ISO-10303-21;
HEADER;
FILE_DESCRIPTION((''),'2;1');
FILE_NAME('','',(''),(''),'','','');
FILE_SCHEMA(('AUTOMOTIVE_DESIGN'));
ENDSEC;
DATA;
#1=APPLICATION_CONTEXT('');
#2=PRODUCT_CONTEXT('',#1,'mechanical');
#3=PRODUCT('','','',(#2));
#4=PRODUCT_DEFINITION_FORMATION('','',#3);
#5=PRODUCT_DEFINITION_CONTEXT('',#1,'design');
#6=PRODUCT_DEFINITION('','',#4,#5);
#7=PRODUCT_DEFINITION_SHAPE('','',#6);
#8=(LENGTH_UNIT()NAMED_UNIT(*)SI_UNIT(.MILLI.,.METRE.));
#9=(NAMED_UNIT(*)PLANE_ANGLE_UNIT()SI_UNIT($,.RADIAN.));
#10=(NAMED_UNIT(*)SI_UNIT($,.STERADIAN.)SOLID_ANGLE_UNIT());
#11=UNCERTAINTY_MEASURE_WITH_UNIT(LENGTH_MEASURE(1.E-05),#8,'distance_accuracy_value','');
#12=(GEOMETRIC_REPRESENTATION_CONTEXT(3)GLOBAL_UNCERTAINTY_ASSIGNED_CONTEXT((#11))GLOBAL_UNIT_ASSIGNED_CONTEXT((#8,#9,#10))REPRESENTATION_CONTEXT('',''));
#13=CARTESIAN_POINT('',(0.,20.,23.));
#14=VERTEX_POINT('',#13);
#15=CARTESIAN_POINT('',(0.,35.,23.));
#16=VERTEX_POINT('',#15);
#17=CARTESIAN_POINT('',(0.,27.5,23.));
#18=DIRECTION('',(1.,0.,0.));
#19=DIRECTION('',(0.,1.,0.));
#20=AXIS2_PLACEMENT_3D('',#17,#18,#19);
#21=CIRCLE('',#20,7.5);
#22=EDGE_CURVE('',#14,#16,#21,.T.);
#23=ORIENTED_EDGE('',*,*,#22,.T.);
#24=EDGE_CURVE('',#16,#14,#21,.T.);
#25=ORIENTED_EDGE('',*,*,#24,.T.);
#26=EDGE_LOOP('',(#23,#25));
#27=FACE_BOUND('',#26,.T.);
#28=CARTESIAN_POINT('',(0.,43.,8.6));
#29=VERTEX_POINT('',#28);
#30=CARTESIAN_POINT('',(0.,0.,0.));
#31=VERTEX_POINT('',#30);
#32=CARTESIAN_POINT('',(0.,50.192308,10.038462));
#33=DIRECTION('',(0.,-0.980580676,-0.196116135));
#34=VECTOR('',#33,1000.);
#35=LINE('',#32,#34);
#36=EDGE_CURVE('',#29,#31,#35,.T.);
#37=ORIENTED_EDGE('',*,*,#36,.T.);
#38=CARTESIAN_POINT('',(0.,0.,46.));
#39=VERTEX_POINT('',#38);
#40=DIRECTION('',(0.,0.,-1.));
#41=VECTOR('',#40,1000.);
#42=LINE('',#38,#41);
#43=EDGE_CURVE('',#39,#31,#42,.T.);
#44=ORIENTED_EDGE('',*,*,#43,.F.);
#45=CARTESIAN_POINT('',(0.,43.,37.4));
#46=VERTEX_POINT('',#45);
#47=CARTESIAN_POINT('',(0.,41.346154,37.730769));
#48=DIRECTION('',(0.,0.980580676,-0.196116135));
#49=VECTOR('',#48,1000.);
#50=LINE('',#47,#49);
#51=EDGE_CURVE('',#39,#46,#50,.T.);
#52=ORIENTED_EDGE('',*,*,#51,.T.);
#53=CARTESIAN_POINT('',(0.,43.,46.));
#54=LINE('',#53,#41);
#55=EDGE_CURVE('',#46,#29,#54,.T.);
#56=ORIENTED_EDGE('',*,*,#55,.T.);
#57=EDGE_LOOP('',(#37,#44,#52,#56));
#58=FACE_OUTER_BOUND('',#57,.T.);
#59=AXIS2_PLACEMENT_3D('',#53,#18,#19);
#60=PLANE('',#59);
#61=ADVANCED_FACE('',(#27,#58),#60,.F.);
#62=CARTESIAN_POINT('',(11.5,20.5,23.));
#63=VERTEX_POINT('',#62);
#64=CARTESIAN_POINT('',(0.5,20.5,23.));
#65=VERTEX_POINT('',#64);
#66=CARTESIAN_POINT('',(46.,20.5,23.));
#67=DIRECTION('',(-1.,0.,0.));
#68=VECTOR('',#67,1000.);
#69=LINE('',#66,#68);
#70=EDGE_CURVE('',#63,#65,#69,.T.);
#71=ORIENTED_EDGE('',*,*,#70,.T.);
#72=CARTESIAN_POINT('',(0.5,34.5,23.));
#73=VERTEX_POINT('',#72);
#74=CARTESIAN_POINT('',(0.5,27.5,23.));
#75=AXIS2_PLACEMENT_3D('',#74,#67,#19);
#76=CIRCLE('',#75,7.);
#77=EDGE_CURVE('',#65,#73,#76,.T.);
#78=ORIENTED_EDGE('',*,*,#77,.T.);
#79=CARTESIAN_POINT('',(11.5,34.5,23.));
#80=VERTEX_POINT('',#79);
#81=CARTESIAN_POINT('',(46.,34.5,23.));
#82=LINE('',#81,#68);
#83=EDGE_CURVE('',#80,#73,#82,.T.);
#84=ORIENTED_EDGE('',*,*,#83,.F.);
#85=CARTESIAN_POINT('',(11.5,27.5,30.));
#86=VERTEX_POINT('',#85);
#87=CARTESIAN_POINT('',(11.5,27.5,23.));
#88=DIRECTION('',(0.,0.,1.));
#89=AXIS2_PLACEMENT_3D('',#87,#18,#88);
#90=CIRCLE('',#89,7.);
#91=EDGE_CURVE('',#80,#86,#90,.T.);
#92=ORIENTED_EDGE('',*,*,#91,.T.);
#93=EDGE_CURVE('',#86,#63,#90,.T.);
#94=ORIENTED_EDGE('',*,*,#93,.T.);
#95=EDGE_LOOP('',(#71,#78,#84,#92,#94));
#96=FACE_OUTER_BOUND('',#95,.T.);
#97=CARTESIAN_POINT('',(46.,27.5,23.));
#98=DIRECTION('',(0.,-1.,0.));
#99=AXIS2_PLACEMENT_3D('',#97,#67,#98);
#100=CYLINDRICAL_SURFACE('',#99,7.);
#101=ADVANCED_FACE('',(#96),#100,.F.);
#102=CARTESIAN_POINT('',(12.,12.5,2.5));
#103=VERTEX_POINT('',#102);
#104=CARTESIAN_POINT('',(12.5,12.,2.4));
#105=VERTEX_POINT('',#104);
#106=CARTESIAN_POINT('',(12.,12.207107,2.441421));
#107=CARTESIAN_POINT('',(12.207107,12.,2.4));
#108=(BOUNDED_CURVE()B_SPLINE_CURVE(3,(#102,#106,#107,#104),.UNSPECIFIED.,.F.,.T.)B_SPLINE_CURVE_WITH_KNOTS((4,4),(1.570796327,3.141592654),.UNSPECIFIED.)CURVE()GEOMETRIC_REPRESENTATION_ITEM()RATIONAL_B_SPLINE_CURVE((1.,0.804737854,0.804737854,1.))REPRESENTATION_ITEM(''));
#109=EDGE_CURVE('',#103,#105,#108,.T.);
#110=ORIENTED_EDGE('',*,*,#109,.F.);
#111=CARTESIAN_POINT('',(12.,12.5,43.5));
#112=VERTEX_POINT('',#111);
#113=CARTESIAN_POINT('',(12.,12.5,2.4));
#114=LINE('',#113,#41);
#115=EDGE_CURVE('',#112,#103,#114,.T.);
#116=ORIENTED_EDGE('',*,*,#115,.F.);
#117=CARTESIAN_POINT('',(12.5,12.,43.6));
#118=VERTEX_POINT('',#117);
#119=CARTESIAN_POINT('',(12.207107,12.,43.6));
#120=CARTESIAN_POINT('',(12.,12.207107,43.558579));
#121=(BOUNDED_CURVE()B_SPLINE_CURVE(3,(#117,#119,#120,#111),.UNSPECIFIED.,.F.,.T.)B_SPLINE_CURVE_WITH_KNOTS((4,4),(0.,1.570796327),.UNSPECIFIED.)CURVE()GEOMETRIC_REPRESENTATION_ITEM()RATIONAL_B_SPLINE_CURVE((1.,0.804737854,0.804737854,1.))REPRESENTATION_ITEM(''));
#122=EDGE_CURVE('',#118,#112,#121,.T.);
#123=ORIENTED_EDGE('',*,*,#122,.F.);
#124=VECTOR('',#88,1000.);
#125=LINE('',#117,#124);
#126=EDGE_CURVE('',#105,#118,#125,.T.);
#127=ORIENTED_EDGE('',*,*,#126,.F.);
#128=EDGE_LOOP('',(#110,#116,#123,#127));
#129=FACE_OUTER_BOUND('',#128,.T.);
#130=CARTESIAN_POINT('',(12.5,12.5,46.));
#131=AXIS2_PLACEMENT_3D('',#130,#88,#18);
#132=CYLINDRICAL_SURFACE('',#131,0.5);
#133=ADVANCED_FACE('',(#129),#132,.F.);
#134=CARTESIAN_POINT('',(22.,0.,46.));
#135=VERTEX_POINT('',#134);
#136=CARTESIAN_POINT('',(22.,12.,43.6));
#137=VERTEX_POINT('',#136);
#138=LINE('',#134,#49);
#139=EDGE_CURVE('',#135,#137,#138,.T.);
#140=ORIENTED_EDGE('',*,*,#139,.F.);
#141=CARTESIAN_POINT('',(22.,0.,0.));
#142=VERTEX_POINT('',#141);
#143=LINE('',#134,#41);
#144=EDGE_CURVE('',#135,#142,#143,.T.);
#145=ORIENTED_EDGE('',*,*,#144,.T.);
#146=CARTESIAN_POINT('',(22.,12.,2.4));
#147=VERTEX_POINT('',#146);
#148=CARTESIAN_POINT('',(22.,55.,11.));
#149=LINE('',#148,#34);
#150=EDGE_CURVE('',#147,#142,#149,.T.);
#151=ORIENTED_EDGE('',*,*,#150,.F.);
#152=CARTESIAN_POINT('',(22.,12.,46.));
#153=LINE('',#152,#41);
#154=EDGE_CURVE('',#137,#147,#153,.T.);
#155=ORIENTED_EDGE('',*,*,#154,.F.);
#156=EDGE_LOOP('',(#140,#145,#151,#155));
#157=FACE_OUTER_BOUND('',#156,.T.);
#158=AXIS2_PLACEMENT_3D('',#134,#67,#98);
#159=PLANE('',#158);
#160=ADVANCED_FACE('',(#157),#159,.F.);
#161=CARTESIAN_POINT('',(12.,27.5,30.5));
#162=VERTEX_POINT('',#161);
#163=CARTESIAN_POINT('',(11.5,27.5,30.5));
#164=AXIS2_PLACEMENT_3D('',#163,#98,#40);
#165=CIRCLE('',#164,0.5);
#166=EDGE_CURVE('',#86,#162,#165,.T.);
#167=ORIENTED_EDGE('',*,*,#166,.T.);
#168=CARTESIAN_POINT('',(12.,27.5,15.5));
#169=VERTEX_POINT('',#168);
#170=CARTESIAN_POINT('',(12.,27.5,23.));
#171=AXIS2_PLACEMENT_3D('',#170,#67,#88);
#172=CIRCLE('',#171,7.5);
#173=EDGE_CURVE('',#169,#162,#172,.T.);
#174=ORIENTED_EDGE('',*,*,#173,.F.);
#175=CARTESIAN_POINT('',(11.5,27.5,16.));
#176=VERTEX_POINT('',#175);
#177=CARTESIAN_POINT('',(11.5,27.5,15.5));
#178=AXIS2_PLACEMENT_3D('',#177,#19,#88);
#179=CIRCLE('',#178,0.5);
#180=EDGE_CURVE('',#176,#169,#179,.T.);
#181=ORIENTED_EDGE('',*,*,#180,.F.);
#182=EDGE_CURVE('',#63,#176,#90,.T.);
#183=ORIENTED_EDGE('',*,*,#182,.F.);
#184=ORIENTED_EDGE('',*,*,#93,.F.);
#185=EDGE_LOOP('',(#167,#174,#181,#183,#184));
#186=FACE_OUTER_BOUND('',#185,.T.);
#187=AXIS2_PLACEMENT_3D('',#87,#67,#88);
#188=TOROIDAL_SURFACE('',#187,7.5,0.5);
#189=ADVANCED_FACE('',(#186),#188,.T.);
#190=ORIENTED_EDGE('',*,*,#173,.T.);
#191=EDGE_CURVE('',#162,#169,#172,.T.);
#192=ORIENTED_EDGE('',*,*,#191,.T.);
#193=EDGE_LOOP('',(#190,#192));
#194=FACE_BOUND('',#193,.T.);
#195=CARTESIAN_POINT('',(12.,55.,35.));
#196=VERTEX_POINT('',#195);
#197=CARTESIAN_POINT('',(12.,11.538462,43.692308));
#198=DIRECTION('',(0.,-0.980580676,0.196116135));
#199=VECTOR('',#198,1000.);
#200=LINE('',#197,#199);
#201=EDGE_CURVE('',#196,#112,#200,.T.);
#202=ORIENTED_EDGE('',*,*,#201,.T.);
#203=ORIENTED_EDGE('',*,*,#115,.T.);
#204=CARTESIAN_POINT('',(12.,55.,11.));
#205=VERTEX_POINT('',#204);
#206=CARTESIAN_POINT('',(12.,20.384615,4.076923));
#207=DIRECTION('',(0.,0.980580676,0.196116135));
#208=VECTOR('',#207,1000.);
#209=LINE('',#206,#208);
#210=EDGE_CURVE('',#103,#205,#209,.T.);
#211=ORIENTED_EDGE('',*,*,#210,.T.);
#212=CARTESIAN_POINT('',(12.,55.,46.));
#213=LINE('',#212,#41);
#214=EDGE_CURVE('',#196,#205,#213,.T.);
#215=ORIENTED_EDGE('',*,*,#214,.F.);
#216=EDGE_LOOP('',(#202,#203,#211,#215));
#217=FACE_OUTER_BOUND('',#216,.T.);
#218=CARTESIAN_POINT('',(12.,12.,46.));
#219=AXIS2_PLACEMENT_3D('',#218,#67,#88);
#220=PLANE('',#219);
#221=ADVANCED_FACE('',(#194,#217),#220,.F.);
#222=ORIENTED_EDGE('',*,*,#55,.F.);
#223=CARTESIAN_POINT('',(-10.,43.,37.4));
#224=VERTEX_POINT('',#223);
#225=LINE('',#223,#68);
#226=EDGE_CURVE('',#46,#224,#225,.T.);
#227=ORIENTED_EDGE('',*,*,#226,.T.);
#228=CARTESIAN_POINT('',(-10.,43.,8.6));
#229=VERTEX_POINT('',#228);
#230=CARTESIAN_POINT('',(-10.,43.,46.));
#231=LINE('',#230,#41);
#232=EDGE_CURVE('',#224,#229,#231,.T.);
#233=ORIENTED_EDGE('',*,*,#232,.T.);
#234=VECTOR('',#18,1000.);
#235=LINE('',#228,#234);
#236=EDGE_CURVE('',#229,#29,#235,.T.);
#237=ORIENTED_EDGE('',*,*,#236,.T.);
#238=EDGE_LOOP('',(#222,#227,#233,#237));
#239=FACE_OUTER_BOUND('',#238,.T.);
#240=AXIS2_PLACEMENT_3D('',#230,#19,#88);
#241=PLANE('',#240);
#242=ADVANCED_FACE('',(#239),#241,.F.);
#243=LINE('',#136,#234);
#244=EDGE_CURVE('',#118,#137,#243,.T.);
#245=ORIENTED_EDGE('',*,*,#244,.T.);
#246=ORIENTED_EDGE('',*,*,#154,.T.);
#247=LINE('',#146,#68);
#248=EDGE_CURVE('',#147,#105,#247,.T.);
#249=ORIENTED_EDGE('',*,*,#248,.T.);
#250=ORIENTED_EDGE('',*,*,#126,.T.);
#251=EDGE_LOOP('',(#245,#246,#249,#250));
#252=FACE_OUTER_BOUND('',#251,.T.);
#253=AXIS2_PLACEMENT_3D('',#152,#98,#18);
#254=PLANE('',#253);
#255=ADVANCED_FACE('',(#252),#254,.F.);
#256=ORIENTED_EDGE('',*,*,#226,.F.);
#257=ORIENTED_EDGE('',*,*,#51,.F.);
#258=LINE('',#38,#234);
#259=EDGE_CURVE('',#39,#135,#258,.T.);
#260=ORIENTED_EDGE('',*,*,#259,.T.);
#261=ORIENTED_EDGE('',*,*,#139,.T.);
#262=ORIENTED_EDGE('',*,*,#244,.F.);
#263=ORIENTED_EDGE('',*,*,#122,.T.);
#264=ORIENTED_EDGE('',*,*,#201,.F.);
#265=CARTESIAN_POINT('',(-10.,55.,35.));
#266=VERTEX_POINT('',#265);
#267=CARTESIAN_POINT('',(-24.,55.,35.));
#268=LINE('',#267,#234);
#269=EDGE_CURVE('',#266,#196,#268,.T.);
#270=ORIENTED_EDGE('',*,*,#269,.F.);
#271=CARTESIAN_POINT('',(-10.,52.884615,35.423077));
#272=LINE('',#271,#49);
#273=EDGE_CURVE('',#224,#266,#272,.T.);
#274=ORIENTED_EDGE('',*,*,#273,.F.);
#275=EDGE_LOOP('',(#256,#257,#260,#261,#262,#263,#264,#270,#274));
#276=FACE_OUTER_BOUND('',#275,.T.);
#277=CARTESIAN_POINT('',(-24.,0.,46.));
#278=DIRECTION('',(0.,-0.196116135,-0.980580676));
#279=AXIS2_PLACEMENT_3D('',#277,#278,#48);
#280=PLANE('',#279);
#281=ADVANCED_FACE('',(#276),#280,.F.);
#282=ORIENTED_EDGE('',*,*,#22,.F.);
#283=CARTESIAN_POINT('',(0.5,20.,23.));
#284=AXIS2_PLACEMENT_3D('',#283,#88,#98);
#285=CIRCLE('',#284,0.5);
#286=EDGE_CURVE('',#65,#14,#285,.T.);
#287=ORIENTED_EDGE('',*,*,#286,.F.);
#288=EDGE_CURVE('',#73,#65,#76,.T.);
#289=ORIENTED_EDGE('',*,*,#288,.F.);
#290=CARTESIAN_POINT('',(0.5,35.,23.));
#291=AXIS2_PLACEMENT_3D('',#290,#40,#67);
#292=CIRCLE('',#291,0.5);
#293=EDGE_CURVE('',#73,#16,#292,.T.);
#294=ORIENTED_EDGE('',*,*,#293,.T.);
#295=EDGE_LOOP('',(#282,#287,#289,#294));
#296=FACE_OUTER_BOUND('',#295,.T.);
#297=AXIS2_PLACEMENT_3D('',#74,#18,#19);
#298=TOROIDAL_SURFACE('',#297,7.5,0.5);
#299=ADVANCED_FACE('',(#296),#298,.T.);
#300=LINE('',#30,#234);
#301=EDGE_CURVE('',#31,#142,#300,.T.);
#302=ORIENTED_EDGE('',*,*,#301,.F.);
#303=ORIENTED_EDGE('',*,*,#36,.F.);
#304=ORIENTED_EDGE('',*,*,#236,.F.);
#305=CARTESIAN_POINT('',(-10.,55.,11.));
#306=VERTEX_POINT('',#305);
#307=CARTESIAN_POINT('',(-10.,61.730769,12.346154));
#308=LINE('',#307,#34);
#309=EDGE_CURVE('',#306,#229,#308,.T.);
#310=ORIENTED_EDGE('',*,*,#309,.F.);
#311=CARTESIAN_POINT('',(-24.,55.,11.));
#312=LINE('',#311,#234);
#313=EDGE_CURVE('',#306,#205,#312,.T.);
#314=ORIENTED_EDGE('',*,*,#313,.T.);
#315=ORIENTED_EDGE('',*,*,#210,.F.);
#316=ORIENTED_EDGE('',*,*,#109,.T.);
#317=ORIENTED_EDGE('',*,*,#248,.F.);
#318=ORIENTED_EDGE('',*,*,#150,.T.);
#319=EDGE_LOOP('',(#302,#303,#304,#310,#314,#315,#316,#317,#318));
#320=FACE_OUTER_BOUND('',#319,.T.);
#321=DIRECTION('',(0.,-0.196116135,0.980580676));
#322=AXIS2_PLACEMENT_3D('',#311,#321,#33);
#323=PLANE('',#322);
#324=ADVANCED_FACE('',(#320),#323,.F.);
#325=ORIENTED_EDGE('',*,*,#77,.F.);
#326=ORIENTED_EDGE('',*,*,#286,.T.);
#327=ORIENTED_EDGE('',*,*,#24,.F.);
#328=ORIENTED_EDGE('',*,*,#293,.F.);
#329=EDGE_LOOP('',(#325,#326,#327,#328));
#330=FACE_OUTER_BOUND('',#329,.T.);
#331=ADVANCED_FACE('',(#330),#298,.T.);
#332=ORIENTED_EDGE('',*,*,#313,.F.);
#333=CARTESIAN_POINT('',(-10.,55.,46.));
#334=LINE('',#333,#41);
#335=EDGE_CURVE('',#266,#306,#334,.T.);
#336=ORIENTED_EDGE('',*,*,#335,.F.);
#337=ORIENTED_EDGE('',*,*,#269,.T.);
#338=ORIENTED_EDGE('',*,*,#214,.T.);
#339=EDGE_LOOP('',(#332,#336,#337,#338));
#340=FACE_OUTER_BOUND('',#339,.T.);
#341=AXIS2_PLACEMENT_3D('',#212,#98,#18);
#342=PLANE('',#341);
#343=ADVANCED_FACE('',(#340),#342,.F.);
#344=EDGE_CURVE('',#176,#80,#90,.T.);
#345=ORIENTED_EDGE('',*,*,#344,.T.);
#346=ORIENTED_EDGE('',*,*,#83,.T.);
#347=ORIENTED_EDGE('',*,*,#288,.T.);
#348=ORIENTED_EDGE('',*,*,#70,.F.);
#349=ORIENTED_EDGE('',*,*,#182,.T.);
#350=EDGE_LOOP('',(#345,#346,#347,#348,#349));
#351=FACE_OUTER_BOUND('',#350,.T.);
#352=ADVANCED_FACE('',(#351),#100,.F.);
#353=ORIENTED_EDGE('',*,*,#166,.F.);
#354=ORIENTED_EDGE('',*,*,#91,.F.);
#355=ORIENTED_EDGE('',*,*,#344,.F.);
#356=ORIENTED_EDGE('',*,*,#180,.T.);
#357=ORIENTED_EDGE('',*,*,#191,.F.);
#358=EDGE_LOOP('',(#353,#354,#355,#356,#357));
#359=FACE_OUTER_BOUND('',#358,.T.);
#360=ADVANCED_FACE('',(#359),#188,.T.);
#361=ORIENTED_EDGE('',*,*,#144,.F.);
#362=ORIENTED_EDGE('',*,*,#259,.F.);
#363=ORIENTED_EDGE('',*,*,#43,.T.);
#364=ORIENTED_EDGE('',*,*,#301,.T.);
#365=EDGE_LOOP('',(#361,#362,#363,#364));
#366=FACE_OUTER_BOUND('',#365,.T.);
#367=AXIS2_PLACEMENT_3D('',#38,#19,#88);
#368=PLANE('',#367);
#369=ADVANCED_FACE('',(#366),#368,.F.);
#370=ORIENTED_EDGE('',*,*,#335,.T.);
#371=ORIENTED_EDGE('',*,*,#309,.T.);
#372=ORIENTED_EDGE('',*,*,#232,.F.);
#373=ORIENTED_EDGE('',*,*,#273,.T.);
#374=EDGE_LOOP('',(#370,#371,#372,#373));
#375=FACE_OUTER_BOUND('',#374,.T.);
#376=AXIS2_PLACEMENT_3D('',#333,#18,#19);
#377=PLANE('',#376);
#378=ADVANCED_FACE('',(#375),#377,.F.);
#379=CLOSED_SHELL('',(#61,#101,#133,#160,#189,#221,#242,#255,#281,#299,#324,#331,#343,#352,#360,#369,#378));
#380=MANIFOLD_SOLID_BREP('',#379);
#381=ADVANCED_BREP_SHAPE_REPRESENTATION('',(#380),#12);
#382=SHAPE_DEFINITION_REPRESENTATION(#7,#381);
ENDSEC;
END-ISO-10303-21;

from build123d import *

# Parameters (mm, degrees)
BRACKET_BODY_DEPTH        = 46
TAPERED_SIDE_CUT_DEPTH    = 46
BORE_SKETCH_R             = 7
THROUGH_BORE_14_DEPTH     = 46
BORE_EDGE_FILLET_R0_5_A_R = 0.5
BORE_EDGE_FILLET_R0_5_B_R = 0.5
STEP_EDGE_FILLET_R0_5_R   = 0.5


with BuildPart() as part:
    # Bracket Profile Sketch → Bracket Body (new body)
    with BuildSketch(Plane.XY):
        Polygon((0, 0), (22, 0), (22, 12), (12, 12), (12, 55), (-10, 55), (-10, 43), (0, 43), align=None)
    extrude(amount=BRACKET_BODY_DEPTH)

    # Taper Cut Sketch → Tapered Side Cut (cut)
    with BuildSketch(Plane(origin=(22, 0, 0), x_dir=(0, 0, -1), z_dir=(1, 0, 0))):
        Polygon((-46, 0), (-35, 55), (-46, 55), align=None)
        Polygon((0, 0), (0, 55), (-11, 55), align=None)
    extrude(amount=-TAPERED_SIDE_CUT_DEPTH, mode=Mode.SUBTRACT)

    # Bore Sketch → Through Bore Ø14 (cut)
    with BuildSketch(Plane.ZY):
        with Locations(Location((23, 27.5, 0), (0, 0, 270))):
            Circle(BORE_SKETCH_R)
    extrude(amount=-THROUGH_BORE_14_DEPTH, mode=Mode.SUBTRACT)

    # Bore Edge Fillet R0.5 A
    bore_edge_fillet_r0_5_a_edges = [part.edges().sort_by_distance(p)[0] for p in [
        (12, 34.5, 23),
    ]]
    fillet(bore_edge_fillet_r0_5_a_edges, radius=BORE_EDGE_FILLET_R0_5_A_R)

    # Bore Edge Fillet R0.5 B
    bore_edge_fillet_r0_5_b_edges = [part.edges().sort_by_distance(p)[0] for p in [
        (0, 34.5, 23),
    ]]
    fillet(bore_edge_fillet_r0_5_b_edges, radius=BORE_EDGE_FILLET_R0_5_B_R)

    # Step Edge Fillet R0.5
    step_edge_fillet_r0_5_edges = [part.edges().sort_by_distance(p)[0] for p in [
        (12, 12, 23),
    ]]
    fillet(step_edge_fillet_r0_5_edges, radius=STEP_EDGE_FILLET_R0_5_R)


solid = part.part
